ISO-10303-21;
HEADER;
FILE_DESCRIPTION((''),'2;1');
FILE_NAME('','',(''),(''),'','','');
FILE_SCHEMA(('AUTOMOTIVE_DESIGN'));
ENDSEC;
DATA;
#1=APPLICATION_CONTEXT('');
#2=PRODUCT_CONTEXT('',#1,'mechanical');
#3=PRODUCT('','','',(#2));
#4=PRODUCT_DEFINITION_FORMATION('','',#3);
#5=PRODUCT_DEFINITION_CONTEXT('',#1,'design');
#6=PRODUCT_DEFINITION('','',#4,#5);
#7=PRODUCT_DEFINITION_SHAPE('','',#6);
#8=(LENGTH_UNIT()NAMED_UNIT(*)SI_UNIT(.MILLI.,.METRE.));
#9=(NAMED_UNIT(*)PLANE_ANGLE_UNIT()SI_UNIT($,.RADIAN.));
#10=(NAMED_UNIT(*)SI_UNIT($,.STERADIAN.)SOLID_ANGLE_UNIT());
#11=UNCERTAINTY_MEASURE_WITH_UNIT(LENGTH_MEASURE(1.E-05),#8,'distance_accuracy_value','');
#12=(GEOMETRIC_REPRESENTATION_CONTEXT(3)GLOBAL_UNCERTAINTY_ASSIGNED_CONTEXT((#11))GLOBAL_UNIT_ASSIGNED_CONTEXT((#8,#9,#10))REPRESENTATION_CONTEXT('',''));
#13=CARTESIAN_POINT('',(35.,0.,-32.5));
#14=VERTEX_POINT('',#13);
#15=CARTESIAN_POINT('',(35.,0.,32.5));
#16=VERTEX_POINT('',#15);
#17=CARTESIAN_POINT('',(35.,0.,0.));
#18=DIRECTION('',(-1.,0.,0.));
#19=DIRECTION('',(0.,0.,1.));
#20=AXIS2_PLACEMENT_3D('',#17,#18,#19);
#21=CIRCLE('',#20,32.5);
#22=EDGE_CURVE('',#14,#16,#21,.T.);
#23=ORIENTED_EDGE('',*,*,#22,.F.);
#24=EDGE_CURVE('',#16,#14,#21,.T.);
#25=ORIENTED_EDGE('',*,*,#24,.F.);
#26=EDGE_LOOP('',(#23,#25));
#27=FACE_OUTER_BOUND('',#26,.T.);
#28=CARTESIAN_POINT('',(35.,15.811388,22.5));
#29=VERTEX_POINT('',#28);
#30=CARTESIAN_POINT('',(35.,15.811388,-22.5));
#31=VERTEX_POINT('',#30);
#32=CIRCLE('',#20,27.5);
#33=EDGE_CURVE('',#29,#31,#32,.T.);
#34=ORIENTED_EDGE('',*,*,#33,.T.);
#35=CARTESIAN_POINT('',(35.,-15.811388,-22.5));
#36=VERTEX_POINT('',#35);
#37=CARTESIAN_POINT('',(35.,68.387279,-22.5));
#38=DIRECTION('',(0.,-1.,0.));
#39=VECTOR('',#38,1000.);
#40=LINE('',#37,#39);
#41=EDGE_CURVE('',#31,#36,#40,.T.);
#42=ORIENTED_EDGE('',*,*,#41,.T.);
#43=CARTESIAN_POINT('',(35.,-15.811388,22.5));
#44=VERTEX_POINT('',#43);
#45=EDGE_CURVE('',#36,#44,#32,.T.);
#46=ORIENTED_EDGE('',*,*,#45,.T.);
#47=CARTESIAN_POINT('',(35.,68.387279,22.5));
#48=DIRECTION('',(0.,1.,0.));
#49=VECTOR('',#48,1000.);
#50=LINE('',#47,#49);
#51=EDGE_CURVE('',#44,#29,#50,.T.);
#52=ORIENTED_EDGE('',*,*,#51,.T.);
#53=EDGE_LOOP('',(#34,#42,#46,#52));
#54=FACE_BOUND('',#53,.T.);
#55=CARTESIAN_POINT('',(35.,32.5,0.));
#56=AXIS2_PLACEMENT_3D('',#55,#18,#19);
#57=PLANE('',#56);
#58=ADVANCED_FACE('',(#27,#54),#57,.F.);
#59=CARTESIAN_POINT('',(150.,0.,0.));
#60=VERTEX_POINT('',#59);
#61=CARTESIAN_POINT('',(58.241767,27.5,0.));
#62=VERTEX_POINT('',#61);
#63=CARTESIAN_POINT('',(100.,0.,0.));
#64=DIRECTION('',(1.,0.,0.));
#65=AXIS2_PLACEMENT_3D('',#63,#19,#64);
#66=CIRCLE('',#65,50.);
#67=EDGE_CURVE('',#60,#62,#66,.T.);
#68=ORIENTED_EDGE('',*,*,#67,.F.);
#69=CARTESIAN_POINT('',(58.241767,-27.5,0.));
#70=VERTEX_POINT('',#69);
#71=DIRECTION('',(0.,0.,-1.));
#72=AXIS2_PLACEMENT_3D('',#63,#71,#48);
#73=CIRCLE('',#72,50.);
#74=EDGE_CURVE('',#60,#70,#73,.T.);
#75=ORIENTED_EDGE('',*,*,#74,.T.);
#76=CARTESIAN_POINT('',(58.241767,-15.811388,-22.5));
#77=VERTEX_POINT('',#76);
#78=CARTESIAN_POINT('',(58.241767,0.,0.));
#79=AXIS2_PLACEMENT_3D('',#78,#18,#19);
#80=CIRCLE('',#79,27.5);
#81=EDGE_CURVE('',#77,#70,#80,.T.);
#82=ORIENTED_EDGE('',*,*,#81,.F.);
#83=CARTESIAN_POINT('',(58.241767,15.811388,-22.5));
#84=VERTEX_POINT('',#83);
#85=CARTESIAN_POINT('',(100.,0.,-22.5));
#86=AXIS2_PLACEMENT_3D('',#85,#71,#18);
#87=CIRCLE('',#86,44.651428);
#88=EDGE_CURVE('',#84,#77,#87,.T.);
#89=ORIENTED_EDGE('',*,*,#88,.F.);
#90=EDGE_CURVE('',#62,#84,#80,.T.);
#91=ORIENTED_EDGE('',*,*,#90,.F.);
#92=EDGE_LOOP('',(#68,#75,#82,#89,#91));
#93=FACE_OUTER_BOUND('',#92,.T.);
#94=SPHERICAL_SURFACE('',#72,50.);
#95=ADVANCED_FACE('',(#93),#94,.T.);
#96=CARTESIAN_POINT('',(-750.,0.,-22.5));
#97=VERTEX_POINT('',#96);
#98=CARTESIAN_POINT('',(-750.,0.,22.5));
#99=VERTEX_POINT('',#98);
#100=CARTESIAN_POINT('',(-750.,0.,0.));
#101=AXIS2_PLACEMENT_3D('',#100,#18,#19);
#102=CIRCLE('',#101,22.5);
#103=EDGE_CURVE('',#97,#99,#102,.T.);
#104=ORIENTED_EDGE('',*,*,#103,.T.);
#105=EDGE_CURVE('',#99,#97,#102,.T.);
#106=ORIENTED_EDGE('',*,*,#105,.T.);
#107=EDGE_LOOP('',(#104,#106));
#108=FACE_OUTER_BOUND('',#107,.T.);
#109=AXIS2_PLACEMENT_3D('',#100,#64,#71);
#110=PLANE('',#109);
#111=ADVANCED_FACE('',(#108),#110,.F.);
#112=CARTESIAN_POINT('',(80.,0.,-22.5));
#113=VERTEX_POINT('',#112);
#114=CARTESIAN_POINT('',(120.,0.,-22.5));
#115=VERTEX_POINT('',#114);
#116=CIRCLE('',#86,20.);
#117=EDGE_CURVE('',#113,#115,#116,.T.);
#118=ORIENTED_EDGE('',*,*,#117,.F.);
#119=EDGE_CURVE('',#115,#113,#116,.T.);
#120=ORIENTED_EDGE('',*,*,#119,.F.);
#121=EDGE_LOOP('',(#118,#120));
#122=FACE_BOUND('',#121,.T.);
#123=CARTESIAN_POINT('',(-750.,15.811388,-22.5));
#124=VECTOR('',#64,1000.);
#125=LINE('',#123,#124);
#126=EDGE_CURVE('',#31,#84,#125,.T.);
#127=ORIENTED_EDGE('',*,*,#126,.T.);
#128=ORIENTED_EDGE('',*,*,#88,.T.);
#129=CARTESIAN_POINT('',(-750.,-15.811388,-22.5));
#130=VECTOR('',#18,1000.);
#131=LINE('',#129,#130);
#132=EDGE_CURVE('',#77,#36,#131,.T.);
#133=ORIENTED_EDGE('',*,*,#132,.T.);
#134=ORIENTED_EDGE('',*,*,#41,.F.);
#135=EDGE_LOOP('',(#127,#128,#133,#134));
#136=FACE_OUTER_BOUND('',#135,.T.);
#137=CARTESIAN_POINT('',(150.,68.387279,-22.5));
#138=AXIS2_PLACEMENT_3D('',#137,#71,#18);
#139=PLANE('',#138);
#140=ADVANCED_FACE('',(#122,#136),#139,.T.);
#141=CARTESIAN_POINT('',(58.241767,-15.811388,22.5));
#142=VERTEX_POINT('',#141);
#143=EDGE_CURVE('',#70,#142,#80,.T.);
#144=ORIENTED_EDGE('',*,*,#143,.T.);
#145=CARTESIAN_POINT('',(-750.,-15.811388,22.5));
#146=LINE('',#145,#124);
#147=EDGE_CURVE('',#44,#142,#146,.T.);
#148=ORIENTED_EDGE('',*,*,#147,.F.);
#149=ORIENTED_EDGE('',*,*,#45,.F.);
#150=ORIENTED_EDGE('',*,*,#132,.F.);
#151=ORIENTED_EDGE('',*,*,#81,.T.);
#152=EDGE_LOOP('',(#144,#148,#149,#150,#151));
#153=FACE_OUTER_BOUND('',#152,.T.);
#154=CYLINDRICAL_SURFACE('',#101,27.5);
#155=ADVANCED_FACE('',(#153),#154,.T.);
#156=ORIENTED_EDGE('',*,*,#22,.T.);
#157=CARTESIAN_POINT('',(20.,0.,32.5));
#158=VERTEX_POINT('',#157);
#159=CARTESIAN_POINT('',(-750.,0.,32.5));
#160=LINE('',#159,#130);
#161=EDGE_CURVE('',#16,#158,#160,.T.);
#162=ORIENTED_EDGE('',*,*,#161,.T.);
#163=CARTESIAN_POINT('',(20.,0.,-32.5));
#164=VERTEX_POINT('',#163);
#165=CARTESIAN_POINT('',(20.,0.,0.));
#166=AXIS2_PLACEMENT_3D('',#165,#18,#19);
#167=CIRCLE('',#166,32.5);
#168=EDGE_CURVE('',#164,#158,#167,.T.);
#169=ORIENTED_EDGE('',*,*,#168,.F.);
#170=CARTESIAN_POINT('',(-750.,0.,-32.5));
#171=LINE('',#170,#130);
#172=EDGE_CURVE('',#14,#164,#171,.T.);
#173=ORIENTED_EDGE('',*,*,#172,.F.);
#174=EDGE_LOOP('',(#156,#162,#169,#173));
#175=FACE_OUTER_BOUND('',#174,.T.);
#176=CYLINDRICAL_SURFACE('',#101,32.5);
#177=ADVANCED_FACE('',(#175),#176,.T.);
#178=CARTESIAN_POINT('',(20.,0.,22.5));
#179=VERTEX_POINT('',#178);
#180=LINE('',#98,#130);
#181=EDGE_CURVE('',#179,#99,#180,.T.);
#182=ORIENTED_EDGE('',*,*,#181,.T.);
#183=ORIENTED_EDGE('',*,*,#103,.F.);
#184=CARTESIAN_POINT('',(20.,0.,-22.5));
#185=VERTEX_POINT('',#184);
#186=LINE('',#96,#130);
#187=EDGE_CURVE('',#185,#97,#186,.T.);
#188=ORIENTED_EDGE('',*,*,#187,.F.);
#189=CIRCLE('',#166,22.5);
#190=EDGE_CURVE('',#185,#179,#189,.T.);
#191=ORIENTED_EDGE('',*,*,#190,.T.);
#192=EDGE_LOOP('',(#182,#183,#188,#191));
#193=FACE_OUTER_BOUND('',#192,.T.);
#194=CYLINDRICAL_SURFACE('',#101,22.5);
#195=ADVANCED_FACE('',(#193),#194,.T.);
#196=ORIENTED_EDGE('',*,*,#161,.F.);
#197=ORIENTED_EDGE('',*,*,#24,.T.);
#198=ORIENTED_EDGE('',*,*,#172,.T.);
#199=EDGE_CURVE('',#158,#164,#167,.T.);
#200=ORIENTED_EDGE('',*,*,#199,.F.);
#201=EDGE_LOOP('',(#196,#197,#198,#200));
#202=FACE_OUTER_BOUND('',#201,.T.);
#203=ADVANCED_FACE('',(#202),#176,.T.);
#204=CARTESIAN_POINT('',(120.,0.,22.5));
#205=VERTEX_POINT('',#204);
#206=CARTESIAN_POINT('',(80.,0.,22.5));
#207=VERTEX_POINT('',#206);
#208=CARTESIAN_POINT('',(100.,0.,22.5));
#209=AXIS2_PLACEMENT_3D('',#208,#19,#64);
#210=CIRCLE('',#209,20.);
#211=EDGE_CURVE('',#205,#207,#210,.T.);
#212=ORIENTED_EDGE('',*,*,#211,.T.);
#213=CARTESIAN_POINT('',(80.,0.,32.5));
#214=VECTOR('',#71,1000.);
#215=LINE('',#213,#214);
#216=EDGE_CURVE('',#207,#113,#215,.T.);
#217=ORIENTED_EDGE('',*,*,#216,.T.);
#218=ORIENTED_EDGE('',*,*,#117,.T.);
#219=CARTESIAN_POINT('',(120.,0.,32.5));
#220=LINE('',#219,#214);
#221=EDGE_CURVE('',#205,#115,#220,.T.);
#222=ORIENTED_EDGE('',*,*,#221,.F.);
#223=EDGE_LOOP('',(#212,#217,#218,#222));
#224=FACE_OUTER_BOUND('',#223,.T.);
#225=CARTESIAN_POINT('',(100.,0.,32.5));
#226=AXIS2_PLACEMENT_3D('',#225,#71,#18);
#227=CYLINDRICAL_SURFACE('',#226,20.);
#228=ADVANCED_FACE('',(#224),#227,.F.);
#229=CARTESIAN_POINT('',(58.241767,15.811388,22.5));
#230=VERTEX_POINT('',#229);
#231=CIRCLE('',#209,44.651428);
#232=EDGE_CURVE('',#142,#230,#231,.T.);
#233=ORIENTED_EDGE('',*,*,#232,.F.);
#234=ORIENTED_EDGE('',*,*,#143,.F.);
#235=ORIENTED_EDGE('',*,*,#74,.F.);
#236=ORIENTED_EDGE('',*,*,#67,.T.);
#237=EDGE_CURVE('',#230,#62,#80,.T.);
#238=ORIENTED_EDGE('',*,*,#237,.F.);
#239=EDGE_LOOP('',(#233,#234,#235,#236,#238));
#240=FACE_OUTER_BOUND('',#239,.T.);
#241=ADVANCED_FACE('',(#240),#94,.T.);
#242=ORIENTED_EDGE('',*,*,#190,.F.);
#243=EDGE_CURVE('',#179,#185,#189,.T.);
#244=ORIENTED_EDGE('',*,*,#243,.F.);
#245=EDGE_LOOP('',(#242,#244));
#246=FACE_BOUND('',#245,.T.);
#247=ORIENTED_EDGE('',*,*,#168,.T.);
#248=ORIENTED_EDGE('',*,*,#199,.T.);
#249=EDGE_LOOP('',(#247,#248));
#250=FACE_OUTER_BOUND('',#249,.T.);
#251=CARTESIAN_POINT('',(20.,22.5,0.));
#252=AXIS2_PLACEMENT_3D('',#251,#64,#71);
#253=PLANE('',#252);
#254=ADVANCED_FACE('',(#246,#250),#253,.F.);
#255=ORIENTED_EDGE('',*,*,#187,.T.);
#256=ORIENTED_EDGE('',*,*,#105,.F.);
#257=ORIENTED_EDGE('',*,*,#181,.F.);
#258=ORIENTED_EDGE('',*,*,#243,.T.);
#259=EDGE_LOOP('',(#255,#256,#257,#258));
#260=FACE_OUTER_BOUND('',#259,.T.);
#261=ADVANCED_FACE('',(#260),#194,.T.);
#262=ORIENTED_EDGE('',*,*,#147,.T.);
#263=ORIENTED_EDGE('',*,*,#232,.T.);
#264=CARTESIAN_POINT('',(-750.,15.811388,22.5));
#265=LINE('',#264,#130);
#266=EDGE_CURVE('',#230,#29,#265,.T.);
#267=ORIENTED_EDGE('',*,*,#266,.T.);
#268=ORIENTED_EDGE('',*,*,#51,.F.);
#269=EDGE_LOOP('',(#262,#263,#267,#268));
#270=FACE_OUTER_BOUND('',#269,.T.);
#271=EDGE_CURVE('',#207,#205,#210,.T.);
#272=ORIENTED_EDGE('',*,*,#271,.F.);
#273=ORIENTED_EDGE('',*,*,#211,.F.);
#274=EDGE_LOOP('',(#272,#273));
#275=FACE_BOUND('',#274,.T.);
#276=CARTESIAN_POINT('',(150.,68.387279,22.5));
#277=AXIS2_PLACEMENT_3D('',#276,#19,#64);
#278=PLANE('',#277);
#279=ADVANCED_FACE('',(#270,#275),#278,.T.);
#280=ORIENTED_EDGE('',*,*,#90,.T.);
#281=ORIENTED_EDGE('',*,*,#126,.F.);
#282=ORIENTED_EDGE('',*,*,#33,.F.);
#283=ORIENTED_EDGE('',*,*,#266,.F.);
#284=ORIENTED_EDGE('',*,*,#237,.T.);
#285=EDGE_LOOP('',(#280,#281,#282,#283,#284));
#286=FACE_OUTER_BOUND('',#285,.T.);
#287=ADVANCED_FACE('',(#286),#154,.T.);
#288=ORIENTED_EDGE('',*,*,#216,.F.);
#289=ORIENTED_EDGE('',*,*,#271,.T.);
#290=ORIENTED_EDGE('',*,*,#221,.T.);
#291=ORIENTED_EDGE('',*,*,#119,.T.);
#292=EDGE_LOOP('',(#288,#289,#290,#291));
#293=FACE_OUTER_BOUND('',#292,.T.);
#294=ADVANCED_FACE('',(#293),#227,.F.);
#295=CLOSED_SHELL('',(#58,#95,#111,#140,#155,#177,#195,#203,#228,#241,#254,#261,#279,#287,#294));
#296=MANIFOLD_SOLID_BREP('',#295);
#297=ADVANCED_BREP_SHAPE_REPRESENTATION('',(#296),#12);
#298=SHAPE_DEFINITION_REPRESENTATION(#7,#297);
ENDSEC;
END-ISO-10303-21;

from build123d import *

# Parameters (mm, degrees)
SKETCH_2_W          = 36.907420495
SKETCH_2_H          = 136.774558304
CUT_EXTRUDE_1_DEPTH = 789.178279325
SKETCH_3_R          = 20
CUT_EXTRUDE_2_DEPTH = 754.674332852


with BuildPart() as part:
    # Sketch 1 → Revolve 1 (revolve)
    with BuildSketch(Plane.XY, mode=Mode.PRIVATE) as revolve_1_sk:
        with BuildLine():
            Line((-750, 0), (-750, 22.5))
            Line((-750, 22.5), (20, 22.5))
            Line((20, 22.5), (20, 32.5))
            Line((20, 32.5), (35, 32.5))
            Line((35, 32.5), (35, 27.5))
            Line((35, 27.5), (58.241767279, 27.5))
            ThreePointArc((58.241767279, 27.5), (114.354239164, 47.895258826), (150, 0))
            Line((150, 0), (-750, 0))
        make_face()
    revolve(revolve_1_sk.sketch.rotate(Axis((-750, 0, 0), (1, 0, 0)), 90), axis=Axis((-750, 0, 0), (1, 0, 0)))

    # Sketch 2 → Cut-Extrude 1 (cut, through all)
    with BuildSketch(Plane(origin=(35, 0, 0), x_dir=(0, 0, -1), z_dir=(1, 0, 0))):
        with Locations((40.953710247, 0)):
            Rectangle(SKETCH_2_W, SKETCH_2_H)
        with Locations((-40.953710247, 0)):
            Rectangle(SKETCH_2_W, SKETCH_2_H)
    extrude(amount=CUT_EXTRUDE_1_DEPTH, mode=Mode.SUBTRACT)

    # Sketch 3 → Cut-Extrude 2 (cut, through all)
    with BuildSketch(Plane(origin=(0, 0, -22.5), x_dir=(-1, 0, 0), z_dir=(0, 0, -1))):
        with Locations((-100, 0)):
            Circle(SKETCH_3_R)
    extrude(amount=-CUT_EXTRUDE_2_DEPTH, mode=Mode.SUBTRACT)


solid = part.part
